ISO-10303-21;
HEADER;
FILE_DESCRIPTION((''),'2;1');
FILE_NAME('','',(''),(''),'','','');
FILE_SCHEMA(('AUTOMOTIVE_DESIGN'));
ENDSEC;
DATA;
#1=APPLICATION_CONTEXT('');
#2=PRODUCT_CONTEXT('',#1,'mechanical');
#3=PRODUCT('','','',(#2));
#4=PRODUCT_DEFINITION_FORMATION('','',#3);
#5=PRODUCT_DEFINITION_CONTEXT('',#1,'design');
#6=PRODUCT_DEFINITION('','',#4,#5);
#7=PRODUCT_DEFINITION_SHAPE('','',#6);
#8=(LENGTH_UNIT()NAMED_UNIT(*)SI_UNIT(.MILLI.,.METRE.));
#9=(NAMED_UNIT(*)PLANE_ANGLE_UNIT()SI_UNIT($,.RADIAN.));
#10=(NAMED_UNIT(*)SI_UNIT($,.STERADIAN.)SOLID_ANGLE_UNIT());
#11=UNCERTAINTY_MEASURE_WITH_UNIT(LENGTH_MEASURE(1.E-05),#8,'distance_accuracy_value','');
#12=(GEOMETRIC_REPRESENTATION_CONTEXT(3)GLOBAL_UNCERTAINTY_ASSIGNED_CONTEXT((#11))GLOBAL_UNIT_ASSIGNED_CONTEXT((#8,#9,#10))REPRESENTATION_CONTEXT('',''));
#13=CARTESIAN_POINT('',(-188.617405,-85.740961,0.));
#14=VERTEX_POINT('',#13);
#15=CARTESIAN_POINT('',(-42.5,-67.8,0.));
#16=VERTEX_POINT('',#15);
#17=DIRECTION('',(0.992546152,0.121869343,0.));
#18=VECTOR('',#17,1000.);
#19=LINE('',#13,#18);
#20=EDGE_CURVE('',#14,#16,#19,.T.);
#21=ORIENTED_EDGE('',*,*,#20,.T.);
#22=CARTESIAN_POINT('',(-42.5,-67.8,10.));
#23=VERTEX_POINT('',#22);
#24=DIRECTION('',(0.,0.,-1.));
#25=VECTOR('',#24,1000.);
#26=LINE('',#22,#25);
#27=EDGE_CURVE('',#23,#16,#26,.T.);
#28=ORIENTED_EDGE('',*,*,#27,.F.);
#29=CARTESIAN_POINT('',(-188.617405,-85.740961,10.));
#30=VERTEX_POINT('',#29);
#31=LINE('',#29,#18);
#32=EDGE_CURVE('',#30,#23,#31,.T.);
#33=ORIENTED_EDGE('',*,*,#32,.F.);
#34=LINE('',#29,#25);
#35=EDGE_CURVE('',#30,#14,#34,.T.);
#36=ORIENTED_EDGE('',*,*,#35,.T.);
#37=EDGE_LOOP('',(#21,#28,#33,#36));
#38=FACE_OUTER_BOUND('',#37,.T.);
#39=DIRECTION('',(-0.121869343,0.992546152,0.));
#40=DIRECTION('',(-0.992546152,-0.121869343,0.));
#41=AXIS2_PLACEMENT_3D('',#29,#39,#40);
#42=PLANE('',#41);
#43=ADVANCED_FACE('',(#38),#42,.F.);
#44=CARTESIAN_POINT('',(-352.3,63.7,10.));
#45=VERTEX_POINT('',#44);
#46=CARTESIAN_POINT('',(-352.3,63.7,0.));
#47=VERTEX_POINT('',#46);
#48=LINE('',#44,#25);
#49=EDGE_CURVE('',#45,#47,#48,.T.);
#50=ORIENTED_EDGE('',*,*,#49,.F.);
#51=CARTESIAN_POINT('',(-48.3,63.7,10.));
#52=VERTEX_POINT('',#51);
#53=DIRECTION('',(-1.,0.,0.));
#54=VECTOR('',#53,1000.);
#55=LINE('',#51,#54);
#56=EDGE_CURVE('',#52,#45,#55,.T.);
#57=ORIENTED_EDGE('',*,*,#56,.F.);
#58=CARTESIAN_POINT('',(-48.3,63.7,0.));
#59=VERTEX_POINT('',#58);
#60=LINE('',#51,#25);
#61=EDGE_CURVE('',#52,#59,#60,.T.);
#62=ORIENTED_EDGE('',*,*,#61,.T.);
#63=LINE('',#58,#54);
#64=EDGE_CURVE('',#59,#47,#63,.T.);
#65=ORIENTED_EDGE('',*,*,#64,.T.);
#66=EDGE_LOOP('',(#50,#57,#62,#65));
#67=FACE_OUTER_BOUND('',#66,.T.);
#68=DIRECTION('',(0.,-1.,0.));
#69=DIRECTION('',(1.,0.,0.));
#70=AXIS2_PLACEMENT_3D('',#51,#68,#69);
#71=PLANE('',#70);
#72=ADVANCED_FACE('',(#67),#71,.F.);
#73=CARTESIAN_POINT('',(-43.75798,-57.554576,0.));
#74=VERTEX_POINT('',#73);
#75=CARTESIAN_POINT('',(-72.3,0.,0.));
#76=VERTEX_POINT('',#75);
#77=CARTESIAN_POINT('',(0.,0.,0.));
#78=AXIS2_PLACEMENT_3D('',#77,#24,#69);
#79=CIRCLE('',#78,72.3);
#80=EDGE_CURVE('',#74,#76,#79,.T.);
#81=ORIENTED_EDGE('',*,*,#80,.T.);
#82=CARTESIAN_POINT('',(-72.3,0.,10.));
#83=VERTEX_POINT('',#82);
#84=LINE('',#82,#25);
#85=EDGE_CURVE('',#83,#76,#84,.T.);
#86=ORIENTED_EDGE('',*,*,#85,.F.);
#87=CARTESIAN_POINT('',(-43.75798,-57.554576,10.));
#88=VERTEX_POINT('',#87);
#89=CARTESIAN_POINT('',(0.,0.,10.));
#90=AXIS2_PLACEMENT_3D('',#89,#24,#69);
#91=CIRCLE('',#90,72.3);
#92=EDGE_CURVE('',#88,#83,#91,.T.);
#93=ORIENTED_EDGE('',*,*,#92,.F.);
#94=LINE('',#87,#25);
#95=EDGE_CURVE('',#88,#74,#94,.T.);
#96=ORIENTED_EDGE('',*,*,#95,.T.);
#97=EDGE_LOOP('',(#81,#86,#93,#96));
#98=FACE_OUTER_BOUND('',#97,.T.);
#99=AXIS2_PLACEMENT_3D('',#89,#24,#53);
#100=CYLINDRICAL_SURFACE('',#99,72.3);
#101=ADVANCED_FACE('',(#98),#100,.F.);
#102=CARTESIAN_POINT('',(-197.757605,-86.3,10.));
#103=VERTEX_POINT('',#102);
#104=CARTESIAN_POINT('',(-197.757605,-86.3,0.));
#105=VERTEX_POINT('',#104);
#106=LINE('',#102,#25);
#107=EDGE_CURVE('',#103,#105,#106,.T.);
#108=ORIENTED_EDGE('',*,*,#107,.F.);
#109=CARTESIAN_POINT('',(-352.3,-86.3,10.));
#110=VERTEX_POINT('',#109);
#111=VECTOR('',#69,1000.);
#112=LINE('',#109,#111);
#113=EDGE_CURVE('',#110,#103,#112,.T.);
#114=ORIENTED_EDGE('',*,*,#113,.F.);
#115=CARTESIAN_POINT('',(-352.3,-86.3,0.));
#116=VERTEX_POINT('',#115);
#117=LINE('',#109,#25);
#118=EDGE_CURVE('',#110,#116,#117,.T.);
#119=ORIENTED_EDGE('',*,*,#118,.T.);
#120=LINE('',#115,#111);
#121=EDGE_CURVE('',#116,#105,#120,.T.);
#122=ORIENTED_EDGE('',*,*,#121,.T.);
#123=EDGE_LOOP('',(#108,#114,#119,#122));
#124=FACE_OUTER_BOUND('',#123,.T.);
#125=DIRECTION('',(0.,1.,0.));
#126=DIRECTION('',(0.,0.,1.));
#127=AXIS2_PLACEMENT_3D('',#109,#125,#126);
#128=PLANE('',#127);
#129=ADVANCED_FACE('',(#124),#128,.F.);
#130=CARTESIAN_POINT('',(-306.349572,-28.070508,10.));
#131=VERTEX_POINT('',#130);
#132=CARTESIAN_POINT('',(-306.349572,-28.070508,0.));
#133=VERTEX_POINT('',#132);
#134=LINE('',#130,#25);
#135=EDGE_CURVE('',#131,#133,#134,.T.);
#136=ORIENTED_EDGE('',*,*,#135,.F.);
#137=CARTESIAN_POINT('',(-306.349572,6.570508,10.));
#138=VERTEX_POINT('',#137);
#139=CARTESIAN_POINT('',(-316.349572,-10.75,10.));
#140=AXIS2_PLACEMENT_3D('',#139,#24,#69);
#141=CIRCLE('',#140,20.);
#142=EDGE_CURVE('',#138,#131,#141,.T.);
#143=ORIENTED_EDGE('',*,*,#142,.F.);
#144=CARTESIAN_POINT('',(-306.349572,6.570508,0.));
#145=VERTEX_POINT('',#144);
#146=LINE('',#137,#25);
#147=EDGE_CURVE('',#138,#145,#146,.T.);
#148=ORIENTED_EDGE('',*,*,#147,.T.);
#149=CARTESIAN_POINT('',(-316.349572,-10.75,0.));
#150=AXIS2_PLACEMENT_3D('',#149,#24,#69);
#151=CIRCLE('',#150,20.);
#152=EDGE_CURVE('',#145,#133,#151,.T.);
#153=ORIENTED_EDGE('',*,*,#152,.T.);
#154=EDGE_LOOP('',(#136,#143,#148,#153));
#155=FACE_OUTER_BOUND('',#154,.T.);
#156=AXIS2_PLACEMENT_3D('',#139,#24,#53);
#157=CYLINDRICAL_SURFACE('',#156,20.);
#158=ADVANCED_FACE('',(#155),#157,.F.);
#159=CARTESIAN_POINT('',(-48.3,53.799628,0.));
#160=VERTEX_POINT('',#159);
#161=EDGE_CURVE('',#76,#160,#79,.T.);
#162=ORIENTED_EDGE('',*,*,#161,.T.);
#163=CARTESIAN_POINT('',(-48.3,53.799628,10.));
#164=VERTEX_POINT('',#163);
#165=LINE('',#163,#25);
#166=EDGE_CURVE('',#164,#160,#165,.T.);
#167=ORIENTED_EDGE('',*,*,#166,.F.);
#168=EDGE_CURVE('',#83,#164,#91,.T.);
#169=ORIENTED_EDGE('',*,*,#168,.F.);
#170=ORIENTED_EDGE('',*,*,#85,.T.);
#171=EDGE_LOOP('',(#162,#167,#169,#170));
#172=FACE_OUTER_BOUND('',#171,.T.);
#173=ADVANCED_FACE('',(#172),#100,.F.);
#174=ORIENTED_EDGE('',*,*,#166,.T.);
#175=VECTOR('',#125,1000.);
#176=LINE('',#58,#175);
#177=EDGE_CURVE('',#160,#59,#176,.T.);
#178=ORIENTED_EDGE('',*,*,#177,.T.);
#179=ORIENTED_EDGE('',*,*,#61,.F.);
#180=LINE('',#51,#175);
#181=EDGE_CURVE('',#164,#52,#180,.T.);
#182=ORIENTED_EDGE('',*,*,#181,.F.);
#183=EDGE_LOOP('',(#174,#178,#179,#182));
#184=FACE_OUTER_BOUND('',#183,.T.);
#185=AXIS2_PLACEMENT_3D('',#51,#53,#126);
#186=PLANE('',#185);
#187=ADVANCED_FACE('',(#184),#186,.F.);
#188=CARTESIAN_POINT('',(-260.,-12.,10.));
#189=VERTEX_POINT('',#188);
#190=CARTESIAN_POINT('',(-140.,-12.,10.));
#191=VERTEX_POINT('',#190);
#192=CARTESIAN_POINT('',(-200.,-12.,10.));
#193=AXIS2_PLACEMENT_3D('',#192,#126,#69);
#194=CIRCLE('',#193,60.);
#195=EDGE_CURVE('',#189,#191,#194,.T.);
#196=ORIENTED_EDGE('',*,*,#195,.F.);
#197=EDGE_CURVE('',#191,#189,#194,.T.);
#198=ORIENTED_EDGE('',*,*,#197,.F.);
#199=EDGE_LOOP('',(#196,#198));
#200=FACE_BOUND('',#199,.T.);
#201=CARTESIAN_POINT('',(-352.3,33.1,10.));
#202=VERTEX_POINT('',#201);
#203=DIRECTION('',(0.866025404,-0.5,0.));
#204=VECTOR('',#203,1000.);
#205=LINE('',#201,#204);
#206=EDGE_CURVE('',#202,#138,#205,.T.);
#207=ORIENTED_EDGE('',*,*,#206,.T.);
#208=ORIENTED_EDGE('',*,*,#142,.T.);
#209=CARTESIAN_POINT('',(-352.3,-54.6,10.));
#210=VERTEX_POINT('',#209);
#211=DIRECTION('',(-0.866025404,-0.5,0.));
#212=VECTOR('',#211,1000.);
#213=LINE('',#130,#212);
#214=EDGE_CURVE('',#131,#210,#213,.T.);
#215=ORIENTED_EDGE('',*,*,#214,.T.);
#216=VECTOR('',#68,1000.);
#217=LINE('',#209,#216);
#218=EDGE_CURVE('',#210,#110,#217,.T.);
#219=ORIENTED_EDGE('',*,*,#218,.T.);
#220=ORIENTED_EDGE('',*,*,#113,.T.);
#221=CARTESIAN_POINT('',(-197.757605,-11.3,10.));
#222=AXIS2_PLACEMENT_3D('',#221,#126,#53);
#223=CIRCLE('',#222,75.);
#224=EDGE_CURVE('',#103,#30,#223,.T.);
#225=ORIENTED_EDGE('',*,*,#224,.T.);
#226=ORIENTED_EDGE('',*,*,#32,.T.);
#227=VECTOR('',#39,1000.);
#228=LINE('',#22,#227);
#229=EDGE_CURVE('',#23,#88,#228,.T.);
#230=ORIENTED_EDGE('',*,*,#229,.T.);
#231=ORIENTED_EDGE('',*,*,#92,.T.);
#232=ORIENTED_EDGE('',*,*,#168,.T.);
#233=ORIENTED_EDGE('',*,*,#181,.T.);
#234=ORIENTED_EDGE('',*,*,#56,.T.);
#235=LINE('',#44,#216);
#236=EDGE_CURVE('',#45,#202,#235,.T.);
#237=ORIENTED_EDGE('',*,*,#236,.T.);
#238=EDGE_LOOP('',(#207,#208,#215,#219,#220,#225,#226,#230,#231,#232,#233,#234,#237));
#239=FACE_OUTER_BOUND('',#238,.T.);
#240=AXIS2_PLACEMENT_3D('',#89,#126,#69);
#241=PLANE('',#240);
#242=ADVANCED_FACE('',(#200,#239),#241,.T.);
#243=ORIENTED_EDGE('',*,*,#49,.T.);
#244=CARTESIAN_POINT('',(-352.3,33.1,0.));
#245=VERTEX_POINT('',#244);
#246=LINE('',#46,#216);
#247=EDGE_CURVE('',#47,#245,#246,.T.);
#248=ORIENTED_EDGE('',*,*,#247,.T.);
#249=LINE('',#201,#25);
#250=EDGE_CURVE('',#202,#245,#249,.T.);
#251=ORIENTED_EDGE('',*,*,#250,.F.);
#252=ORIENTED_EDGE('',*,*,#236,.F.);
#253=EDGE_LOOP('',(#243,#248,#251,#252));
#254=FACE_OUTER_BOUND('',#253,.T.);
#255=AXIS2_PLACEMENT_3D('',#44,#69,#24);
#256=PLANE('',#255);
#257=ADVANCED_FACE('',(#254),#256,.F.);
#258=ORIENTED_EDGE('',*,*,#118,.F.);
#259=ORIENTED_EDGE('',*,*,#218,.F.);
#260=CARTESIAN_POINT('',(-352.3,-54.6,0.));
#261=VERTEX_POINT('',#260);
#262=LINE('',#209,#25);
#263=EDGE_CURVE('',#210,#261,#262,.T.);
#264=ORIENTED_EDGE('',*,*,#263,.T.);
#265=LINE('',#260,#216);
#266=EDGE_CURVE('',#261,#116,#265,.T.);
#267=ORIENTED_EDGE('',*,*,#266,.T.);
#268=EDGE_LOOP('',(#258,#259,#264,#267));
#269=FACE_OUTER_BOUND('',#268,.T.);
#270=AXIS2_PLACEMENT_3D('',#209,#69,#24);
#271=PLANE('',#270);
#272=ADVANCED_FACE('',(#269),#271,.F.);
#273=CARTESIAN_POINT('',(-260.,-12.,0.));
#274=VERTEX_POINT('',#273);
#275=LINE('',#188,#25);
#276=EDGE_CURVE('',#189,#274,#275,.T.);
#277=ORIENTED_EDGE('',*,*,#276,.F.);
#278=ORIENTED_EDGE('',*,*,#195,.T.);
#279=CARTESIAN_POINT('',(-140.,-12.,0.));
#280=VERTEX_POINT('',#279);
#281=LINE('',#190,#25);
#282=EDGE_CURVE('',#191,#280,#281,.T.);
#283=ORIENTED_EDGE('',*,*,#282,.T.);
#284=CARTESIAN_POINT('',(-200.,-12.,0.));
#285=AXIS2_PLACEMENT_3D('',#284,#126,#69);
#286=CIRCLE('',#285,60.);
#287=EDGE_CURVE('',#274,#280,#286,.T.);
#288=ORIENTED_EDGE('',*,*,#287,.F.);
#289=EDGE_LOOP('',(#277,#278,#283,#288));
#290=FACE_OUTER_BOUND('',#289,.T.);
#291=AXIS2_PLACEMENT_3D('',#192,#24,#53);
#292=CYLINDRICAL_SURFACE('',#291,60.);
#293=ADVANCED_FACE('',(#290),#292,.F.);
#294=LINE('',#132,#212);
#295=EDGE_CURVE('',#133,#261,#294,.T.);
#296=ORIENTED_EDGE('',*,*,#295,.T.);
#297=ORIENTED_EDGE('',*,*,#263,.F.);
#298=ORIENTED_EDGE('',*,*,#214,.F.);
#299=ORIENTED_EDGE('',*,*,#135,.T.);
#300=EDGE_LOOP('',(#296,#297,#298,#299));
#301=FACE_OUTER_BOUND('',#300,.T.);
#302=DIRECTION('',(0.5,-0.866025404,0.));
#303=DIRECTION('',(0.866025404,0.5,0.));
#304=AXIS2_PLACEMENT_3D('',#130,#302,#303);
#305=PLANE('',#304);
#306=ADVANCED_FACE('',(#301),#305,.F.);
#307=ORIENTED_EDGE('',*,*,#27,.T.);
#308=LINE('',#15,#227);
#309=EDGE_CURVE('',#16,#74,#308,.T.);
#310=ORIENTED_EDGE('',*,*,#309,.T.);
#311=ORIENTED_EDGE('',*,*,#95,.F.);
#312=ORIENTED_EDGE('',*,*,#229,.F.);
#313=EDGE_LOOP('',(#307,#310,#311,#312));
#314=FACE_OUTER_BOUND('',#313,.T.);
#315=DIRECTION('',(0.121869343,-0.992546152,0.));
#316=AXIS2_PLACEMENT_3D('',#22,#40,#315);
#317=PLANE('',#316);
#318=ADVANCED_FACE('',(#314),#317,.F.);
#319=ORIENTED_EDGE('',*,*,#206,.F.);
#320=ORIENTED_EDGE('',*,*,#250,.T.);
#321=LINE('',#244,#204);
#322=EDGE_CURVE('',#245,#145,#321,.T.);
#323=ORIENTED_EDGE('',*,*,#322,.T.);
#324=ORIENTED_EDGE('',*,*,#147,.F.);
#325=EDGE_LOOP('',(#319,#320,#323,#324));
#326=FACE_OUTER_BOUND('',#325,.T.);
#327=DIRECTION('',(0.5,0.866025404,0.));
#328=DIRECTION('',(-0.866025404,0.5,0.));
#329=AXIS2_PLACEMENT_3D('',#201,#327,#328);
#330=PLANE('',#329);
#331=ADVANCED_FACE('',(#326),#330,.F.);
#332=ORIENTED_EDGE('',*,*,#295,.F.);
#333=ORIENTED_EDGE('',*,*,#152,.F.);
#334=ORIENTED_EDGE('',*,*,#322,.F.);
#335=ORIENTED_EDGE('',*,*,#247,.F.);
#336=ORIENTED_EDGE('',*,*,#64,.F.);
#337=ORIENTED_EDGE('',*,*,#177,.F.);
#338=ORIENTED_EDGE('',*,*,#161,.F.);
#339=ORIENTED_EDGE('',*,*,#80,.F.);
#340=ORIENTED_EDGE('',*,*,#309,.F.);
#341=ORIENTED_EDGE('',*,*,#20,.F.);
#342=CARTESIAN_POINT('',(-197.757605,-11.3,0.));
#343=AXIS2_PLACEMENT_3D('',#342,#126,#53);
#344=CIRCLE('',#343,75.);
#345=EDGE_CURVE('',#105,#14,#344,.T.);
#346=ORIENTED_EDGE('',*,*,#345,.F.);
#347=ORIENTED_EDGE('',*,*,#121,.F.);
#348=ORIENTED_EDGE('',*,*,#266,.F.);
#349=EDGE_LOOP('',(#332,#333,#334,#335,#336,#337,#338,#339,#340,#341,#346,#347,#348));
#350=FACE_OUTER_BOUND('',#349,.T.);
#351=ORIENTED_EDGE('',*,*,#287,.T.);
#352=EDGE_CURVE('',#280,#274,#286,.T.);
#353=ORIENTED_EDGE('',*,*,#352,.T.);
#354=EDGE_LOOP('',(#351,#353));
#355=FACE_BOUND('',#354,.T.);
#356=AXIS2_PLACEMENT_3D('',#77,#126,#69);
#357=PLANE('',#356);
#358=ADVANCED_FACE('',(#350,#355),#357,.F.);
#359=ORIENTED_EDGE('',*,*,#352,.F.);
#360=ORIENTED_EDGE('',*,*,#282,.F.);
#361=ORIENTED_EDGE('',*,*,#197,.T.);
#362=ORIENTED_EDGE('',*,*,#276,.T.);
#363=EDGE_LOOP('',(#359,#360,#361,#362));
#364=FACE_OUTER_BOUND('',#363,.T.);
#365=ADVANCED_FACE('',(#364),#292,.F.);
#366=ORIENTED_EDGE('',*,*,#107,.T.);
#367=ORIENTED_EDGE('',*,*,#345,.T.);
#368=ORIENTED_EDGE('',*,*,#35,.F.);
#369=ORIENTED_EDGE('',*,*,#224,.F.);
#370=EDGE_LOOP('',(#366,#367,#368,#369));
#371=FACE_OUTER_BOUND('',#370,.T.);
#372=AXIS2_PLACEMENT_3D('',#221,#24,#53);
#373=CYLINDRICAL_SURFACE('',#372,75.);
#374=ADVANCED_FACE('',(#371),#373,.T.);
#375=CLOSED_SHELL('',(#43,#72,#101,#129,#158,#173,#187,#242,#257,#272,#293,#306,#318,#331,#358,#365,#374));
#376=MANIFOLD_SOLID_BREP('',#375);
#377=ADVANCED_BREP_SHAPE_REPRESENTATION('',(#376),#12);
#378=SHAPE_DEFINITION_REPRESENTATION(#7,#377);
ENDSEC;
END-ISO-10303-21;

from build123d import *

# Parameters (mm, degrees)
SKETCH1_R           = 60
BOSS_EXTRUDE1_DEPTH = 10


with BuildPart() as part:
    # Sketch1 → Boss-Extrude1 (new body)
    with BuildSketch(Plane.XY):
        with BuildLine():
            Line((-48.3, 63.7), (-48.3, 53.799628252))
            ThreePointArc((-48.3, 53.799628252), (-72.239930825, -2.946590294), (-43.757979913, -57.554575786))
            Line((-43.757979913, -57.554575786), (-42.5, -67.8))
            Line((-42.5, -67.8), (-188.617404673, -85.740961373))
            ThreePointArc((-188.617404673, -85.740961373), (-193.178964964, -86.160109882), (-197.757605429, -86.3))
            Line((-197.757605429, -86.3), (-352.3, -86.3))
            Line((-352.3, -86.3), (-352.3, -54.6))
            Line((-352.3, -54.6), (-306.349572088, -28.070508076))
            ThreePointArc((-306.349572088, -28.070508076), (-296.349572088, -10.75), (-306.349572088, 6.570508076))
            Line((-306.349572088, 6.570508076), (-352.3, 33.1))
            Line((-352.3, 33.1), (-352.3, 63.7))
            Line((-352.3, 63.7), (-48.3, 63.7))
        make_face()
        with Locations((-200, -12)):
            Circle(SKETCH1_R, mode=Mode.SUBTRACT)
    extrude(amount=BOSS_EXTRUDE1_DEPTH)


solid = part.part
